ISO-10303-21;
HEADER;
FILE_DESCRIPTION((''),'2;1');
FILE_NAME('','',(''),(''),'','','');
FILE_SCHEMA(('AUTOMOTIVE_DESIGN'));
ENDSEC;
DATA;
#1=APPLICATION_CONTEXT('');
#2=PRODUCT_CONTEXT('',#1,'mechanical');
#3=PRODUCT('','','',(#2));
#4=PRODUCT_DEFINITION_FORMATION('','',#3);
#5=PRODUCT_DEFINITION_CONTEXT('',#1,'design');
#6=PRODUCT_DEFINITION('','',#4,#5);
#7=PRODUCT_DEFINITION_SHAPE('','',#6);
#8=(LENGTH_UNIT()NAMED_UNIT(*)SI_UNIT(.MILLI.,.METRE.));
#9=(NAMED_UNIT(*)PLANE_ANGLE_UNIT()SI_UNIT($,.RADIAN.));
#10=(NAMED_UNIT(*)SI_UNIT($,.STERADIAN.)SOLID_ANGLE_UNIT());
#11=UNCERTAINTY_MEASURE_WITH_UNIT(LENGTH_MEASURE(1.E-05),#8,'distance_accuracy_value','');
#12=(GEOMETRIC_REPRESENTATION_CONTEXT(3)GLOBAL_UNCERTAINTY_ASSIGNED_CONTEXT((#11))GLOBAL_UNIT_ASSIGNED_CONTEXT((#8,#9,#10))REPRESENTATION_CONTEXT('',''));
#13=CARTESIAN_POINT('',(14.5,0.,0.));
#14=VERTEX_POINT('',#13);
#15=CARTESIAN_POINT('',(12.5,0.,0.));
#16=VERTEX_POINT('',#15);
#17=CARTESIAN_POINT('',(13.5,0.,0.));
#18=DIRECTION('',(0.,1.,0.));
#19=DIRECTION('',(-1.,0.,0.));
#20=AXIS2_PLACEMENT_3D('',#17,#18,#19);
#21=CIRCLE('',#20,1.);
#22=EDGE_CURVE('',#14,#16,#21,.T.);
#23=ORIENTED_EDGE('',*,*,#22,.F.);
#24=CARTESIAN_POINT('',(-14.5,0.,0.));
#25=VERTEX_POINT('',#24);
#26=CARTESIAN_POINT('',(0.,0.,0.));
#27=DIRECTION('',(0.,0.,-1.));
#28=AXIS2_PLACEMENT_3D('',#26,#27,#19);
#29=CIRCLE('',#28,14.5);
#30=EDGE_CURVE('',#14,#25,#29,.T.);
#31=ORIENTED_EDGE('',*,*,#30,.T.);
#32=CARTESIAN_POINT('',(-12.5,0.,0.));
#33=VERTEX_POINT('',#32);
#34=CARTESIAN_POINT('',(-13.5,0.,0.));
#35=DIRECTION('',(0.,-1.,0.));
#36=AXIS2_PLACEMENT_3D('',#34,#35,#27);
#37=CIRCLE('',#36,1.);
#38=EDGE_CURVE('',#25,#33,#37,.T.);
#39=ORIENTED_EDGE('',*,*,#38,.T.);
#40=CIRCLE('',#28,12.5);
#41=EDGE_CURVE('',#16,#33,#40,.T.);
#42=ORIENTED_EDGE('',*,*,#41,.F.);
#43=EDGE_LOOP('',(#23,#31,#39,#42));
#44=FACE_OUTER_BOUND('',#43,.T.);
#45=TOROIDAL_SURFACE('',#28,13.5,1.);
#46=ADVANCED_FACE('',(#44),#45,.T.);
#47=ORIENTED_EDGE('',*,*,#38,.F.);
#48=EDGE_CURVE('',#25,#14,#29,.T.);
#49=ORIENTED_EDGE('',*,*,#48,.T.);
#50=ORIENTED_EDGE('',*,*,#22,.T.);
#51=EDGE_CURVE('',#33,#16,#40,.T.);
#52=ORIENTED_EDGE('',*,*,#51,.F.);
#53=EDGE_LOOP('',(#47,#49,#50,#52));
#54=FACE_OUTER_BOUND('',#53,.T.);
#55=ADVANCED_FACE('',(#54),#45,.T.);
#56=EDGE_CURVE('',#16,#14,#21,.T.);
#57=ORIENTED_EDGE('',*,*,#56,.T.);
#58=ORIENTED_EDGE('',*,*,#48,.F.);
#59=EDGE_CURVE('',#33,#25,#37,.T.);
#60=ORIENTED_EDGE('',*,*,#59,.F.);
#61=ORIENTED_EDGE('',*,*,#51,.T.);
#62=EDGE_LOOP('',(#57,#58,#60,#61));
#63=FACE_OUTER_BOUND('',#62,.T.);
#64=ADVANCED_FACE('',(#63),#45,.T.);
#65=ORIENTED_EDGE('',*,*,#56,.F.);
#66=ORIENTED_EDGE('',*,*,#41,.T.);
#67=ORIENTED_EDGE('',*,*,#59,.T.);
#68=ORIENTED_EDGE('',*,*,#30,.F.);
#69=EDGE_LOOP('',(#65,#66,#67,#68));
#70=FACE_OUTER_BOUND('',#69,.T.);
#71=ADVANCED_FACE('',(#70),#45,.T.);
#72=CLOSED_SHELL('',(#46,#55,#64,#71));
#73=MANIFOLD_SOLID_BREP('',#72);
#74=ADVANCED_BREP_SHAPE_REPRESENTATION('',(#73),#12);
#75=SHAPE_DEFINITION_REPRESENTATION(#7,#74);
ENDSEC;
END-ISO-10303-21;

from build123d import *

# Parameters (mm, degrees)
SKETCH1_R = 1


with BuildPart() as part:
    # Sketch1 → Revolve1 (revolve)
    with BuildSketch(Plane(origin=(0, 0, 0), x_dir=(1, 0, 0), z_dir=(0, 1, 0))):
        with Locations((-13.5, 0)):
            Circle(SKETCH1_R)
    revolve(axis=Axis((0, 0, 0), (0, 0, 1)))


solid = part.part
